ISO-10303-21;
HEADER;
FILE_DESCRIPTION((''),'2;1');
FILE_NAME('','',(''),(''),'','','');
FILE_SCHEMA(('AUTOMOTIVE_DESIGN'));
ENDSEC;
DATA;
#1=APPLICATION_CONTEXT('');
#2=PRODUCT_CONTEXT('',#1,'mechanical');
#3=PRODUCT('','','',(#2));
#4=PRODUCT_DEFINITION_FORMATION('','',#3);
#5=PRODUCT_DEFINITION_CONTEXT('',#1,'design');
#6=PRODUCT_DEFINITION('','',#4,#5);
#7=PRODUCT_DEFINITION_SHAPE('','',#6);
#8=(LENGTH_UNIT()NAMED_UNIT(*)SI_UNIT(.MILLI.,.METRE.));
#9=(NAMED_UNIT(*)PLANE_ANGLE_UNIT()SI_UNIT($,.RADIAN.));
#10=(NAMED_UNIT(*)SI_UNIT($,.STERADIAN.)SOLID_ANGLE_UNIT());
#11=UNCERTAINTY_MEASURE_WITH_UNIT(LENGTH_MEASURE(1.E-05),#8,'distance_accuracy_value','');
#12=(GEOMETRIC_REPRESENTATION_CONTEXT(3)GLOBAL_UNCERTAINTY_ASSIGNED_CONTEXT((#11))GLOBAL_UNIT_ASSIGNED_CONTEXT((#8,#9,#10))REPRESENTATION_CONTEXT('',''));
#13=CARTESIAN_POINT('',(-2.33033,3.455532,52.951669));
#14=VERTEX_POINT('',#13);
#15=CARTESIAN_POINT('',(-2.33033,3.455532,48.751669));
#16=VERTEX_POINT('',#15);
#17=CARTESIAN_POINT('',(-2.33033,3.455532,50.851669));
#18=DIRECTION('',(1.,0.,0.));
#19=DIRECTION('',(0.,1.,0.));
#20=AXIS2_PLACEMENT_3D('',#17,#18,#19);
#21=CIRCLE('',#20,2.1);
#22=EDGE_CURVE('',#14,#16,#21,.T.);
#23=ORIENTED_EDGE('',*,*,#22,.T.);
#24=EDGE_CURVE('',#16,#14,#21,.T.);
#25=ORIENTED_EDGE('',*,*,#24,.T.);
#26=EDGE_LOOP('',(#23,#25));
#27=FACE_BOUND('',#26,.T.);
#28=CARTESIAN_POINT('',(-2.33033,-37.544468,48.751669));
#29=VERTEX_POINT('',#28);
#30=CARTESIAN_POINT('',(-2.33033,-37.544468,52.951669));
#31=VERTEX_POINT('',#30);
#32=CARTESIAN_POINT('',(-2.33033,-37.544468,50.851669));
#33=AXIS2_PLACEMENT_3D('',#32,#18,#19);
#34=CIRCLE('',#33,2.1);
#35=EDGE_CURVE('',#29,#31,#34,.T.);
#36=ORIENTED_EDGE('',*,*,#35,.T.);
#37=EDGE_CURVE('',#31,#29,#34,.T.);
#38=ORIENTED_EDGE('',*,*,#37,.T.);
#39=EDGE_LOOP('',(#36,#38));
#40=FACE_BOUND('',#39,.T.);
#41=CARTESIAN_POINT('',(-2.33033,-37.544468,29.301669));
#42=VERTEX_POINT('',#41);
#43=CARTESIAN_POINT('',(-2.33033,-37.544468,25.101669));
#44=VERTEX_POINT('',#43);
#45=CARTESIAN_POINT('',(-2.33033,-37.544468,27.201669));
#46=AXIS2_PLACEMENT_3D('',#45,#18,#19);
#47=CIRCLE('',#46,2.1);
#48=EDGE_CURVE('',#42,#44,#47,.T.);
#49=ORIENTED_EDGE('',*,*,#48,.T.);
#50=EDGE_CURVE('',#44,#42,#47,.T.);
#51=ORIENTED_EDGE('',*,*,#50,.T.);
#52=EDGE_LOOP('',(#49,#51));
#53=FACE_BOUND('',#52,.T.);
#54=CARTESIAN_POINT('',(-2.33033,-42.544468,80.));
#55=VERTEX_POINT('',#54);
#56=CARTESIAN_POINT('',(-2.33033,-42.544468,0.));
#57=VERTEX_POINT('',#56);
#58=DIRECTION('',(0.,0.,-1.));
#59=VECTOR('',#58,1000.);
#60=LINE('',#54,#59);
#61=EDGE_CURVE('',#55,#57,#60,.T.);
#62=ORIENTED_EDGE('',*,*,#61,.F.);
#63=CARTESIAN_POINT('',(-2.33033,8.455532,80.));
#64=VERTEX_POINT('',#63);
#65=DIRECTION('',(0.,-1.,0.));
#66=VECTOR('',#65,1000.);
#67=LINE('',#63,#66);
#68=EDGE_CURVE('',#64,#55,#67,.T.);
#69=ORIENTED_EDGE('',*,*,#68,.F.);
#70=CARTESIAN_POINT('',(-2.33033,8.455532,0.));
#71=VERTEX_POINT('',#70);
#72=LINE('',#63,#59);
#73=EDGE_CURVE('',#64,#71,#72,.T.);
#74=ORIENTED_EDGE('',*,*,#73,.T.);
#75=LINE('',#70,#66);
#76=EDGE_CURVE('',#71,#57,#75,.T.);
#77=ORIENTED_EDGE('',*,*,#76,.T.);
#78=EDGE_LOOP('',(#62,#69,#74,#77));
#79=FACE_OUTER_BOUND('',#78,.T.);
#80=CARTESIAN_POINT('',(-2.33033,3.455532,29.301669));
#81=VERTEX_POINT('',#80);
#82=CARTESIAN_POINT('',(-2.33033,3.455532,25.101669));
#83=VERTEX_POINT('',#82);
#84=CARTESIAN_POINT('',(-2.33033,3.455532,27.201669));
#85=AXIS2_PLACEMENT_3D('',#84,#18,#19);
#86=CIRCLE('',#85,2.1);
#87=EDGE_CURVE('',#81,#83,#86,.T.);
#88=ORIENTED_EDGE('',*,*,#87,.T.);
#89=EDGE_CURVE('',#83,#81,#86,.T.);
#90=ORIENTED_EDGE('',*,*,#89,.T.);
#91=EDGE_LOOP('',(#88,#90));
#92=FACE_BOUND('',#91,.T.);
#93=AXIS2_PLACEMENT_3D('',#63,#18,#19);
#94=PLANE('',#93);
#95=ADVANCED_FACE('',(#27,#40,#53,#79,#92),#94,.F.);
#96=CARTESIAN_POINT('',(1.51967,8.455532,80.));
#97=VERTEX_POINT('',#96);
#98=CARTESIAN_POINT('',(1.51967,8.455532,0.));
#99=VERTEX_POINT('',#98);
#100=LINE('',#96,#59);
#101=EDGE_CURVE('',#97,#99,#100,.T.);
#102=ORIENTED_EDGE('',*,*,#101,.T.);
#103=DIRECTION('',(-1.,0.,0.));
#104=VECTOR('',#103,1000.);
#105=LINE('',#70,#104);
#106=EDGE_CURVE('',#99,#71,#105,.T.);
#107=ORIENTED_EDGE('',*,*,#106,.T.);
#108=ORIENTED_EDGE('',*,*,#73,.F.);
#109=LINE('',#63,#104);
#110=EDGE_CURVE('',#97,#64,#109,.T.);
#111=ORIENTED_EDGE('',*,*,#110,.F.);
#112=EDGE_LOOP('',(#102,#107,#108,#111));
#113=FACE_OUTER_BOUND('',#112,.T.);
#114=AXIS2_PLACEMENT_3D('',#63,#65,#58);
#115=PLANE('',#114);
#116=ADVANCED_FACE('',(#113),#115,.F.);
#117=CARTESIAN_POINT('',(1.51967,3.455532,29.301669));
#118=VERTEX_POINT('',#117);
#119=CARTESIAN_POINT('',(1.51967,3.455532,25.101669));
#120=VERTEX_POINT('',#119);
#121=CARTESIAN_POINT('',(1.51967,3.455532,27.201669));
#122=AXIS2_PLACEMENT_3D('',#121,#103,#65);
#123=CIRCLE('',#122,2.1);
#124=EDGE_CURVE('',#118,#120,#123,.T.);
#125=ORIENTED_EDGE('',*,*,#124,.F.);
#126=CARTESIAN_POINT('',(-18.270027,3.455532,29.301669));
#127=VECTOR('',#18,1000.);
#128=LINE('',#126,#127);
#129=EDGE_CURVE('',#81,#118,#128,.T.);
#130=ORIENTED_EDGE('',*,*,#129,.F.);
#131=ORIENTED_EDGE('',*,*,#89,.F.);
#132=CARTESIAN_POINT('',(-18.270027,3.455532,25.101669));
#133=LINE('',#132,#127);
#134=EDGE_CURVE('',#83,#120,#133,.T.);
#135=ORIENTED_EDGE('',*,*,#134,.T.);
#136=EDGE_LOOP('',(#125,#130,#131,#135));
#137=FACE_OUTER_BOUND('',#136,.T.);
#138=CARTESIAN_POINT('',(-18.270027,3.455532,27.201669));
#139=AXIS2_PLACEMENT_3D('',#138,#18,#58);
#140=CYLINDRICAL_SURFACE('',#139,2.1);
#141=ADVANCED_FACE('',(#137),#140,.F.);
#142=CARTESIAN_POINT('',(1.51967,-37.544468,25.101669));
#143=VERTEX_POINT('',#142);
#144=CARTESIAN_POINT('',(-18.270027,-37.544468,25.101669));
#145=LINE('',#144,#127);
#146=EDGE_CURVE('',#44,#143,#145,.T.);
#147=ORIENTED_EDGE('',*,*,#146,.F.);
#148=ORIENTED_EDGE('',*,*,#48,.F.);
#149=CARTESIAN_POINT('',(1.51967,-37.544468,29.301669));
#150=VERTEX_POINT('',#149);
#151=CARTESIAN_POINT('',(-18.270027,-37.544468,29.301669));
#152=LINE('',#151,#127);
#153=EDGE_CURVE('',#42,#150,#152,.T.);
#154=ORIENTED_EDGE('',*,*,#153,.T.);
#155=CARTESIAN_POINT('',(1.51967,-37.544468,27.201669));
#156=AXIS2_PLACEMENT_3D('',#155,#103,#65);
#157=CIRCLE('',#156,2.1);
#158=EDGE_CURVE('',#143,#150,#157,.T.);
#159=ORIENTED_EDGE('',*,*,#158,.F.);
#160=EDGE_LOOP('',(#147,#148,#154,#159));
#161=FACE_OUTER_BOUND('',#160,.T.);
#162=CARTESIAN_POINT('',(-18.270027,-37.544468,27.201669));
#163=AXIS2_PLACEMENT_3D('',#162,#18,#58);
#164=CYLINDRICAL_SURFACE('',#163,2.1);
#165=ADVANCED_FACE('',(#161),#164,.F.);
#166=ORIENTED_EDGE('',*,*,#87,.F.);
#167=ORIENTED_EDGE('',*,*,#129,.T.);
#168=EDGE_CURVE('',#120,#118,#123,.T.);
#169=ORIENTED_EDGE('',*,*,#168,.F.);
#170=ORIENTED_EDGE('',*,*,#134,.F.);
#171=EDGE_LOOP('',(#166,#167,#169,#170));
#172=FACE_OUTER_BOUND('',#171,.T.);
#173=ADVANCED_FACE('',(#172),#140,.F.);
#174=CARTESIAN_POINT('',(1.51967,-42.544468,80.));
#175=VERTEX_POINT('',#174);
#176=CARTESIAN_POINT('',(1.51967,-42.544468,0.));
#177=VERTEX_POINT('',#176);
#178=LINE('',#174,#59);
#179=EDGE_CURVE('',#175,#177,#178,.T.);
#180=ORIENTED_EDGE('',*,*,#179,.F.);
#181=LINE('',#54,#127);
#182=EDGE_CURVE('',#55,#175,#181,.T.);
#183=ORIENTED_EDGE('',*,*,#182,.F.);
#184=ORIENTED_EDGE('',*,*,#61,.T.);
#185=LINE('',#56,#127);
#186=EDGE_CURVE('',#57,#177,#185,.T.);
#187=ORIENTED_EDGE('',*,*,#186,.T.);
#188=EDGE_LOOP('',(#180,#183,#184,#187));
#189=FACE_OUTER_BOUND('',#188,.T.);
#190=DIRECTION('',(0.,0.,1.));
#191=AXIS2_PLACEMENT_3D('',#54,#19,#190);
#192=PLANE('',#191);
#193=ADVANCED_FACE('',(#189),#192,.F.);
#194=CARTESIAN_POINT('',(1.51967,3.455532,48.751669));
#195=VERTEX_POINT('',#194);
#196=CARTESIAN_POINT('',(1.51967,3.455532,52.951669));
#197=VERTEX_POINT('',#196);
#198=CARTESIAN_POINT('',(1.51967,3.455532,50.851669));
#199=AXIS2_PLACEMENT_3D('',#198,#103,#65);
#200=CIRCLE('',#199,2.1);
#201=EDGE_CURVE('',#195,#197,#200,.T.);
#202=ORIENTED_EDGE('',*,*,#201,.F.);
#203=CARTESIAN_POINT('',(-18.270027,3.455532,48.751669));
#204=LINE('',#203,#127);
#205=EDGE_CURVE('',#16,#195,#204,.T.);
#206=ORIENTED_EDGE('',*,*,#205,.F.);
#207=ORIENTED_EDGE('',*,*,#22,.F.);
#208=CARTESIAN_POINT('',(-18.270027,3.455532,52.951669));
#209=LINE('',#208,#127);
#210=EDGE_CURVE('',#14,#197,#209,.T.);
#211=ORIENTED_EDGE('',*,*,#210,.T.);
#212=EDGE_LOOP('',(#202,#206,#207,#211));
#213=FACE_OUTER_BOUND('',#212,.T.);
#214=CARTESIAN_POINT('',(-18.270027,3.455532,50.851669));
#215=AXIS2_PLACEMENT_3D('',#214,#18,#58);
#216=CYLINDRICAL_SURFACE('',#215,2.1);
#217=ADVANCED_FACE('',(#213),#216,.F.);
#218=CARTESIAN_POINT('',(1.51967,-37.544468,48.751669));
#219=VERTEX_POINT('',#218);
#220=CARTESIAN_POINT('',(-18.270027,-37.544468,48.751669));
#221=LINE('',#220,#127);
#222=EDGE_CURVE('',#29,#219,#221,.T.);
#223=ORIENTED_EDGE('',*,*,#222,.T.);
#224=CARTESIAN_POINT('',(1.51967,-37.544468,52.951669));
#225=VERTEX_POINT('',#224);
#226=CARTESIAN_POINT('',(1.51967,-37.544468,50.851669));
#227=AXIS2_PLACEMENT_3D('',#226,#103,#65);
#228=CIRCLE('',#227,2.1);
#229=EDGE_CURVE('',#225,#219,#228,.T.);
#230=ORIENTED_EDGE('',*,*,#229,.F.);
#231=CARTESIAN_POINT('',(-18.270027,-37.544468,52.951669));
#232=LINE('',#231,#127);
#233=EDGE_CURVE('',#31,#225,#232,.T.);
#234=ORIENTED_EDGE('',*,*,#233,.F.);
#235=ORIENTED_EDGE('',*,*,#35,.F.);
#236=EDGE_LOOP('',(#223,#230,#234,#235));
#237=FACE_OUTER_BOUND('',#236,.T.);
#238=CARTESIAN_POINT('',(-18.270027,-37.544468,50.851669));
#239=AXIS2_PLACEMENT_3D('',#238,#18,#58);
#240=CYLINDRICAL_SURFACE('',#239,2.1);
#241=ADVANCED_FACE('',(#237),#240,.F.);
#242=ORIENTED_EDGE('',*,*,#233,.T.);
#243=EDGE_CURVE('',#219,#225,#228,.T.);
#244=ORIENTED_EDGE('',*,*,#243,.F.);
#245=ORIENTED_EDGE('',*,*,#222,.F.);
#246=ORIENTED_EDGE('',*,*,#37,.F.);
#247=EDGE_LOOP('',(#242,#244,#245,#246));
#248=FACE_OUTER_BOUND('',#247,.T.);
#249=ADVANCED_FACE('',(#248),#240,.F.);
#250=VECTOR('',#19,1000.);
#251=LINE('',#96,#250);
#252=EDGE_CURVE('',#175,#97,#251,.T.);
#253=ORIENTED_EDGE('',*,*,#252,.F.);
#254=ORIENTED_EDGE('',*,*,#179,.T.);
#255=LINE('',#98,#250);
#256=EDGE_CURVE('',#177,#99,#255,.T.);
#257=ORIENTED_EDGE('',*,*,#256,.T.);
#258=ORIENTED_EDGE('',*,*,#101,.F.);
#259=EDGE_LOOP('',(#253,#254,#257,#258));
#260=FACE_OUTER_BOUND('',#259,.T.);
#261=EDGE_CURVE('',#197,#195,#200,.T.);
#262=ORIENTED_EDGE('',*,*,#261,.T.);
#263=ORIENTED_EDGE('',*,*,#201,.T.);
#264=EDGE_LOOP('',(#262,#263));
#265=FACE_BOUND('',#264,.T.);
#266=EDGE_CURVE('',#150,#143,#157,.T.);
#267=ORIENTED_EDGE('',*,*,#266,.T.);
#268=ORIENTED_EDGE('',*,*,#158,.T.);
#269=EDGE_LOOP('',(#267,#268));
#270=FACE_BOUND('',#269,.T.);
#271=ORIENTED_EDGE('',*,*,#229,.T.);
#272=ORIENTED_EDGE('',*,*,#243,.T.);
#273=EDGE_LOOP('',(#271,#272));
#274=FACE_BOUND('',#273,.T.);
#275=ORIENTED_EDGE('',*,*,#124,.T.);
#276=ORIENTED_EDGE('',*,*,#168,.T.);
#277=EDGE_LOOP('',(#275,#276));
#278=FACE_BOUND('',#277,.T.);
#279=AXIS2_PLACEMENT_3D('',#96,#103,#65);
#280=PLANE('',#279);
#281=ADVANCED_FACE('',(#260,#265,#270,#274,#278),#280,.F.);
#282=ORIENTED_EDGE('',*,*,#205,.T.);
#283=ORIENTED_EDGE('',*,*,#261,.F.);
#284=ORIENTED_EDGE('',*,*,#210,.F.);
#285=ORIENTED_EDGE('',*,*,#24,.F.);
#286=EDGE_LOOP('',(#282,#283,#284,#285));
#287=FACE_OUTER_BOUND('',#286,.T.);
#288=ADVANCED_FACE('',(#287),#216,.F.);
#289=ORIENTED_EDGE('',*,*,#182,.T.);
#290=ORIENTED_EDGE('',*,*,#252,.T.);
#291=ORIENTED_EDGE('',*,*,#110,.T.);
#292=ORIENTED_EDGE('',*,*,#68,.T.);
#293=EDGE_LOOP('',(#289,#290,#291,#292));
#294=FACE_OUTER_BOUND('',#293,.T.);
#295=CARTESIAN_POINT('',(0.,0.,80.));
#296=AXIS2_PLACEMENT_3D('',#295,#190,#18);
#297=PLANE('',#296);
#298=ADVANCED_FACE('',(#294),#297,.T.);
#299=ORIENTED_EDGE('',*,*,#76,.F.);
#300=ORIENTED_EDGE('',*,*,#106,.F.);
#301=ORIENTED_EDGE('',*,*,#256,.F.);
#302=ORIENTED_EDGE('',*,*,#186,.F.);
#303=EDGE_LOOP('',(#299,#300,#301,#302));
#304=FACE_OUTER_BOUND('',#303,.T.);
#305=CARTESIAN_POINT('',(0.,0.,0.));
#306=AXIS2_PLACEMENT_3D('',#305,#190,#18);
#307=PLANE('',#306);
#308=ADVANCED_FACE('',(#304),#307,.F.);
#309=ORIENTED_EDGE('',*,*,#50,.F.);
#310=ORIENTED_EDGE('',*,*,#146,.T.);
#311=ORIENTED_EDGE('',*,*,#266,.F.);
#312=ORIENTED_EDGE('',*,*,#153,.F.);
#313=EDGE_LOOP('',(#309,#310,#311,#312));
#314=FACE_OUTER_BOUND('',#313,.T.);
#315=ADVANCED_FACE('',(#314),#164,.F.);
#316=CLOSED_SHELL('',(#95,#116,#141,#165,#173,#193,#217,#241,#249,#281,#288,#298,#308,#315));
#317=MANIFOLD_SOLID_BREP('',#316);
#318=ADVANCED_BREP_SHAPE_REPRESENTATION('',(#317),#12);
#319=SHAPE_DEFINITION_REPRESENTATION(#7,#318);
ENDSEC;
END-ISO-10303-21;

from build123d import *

# Parameters (mm, degrees)
SKETCH_1_W          = 3.85
SKETCH_1_H          = 51
EXTRUDE_1_DEPTH     = 80
CUT_EXTRUDE_1_REACH = 1465.749
SKETCH_2_R          = 2.1


with BuildPart() as part:
    # 草图1 → 凸台-拉伸1 (new body)
    with BuildSketch(Plane.XY):
        with Locations((-0.405329913, -17.044468303)):
            Rectangle(SKETCH_1_W, SKETCH_1_H)
    extrude(amount=EXTRUDE_1_DEPTH)

    # 草图2 → 切除-拉伸1 (cut, up to next)
    with BuildSketch(Plane(origin=(5.369670087, -1051.794731348, 1009.143932915), x_dir=(0, -1, 0), z_dir=(1, 0, 0)), mode=Mode.PRIVATE) as cut_extrude_1_sk1:
        with Locations((-1055.250263055, 981.942263912)):
            Circle(SKETCH_2_R)
    cut_extrude_1_tool1 = extrude(cut_extrude_1_sk1.sketch, amount=-CUT_EXTRUDE_1_REACH, mode=Mode.PRIVATE) & part.part
    # 草图2 → 切除-拉伸1 (cut, up to next)
    with BuildSketch(Plane(origin=(5.369670087, -1051.794731348, 1009.143932915), x_dir=(0, -1, 0), z_dir=(1, 0, 0)), mode=Mode.PRIVATE) as cut_extrude_1_sk2:
        with Locations((-1055.250263055, 958.292263912)):
            Circle(SKETCH_2_R)
    cut_extrude_1_tool2 = extrude(cut_extrude_1_sk2.sketch, amount=-CUT_EXTRUDE_1_REACH, mode=Mode.PRIVATE) & part.part
    # 草图2 → 切除-拉伸1 (cut, up to next)
    with BuildSketch(Plane(origin=(5.369670087, -1051.794731348, 1009.143932915), x_dir=(0, -1, 0), z_dir=(1, 0, 0)), mode=Mode.PRIVATE) as cut_extrude_1_sk3:
        with Locations((-1014.250263055, 958.292263912)):
            Circle(SKETCH_2_R)
    cut_extrude_1_tool3 = extrude(cut_extrude_1_sk3.sketch, amount=-CUT_EXTRUDE_1_REACH, mode=Mode.PRIVATE) & part.part
    # 草图2 → 切除-拉伸1 (cut, up to next)
    with BuildSketch(Plane(origin=(5.369670087, -1051.794731348, 1009.143932915), x_dir=(0, -1, 0), z_dir=(1, 0, 0)), mode=Mode.PRIVATE) as cut_extrude_1_sk4:
        with Locations((-1014.250263055, 981.942263912)):
            Circle(SKETCH_2_R)
    cut_extrude_1_tool4 = extrude(cut_extrude_1_sk4.sketch, amount=-CUT_EXTRUDE_1_REACH, mode=Mode.PRIVATE) & part.part
    add(cut_extrude_1_tool1.solids().sort_by_distance((5.36967, 3.455532, 27.201669))[0], mode=Mode.SUBTRACT)
    add(cut_extrude_1_tool2.solids().sort_by_distance((5.36967, 3.455532, 50.851669))[0], mode=Mode.SUBTRACT)
    add(cut_extrude_1_tool3.solids().sort_by_distance((5.36967, -37.544468, 50.851669))[0], mode=Mode.SUBTRACT)
    add(cut_extrude_1_tool4.solids().sort_by_distance((5.36967, -37.544468, 27.201669))[0], mode=Mode.SUBTRACT)


solid = part.part
